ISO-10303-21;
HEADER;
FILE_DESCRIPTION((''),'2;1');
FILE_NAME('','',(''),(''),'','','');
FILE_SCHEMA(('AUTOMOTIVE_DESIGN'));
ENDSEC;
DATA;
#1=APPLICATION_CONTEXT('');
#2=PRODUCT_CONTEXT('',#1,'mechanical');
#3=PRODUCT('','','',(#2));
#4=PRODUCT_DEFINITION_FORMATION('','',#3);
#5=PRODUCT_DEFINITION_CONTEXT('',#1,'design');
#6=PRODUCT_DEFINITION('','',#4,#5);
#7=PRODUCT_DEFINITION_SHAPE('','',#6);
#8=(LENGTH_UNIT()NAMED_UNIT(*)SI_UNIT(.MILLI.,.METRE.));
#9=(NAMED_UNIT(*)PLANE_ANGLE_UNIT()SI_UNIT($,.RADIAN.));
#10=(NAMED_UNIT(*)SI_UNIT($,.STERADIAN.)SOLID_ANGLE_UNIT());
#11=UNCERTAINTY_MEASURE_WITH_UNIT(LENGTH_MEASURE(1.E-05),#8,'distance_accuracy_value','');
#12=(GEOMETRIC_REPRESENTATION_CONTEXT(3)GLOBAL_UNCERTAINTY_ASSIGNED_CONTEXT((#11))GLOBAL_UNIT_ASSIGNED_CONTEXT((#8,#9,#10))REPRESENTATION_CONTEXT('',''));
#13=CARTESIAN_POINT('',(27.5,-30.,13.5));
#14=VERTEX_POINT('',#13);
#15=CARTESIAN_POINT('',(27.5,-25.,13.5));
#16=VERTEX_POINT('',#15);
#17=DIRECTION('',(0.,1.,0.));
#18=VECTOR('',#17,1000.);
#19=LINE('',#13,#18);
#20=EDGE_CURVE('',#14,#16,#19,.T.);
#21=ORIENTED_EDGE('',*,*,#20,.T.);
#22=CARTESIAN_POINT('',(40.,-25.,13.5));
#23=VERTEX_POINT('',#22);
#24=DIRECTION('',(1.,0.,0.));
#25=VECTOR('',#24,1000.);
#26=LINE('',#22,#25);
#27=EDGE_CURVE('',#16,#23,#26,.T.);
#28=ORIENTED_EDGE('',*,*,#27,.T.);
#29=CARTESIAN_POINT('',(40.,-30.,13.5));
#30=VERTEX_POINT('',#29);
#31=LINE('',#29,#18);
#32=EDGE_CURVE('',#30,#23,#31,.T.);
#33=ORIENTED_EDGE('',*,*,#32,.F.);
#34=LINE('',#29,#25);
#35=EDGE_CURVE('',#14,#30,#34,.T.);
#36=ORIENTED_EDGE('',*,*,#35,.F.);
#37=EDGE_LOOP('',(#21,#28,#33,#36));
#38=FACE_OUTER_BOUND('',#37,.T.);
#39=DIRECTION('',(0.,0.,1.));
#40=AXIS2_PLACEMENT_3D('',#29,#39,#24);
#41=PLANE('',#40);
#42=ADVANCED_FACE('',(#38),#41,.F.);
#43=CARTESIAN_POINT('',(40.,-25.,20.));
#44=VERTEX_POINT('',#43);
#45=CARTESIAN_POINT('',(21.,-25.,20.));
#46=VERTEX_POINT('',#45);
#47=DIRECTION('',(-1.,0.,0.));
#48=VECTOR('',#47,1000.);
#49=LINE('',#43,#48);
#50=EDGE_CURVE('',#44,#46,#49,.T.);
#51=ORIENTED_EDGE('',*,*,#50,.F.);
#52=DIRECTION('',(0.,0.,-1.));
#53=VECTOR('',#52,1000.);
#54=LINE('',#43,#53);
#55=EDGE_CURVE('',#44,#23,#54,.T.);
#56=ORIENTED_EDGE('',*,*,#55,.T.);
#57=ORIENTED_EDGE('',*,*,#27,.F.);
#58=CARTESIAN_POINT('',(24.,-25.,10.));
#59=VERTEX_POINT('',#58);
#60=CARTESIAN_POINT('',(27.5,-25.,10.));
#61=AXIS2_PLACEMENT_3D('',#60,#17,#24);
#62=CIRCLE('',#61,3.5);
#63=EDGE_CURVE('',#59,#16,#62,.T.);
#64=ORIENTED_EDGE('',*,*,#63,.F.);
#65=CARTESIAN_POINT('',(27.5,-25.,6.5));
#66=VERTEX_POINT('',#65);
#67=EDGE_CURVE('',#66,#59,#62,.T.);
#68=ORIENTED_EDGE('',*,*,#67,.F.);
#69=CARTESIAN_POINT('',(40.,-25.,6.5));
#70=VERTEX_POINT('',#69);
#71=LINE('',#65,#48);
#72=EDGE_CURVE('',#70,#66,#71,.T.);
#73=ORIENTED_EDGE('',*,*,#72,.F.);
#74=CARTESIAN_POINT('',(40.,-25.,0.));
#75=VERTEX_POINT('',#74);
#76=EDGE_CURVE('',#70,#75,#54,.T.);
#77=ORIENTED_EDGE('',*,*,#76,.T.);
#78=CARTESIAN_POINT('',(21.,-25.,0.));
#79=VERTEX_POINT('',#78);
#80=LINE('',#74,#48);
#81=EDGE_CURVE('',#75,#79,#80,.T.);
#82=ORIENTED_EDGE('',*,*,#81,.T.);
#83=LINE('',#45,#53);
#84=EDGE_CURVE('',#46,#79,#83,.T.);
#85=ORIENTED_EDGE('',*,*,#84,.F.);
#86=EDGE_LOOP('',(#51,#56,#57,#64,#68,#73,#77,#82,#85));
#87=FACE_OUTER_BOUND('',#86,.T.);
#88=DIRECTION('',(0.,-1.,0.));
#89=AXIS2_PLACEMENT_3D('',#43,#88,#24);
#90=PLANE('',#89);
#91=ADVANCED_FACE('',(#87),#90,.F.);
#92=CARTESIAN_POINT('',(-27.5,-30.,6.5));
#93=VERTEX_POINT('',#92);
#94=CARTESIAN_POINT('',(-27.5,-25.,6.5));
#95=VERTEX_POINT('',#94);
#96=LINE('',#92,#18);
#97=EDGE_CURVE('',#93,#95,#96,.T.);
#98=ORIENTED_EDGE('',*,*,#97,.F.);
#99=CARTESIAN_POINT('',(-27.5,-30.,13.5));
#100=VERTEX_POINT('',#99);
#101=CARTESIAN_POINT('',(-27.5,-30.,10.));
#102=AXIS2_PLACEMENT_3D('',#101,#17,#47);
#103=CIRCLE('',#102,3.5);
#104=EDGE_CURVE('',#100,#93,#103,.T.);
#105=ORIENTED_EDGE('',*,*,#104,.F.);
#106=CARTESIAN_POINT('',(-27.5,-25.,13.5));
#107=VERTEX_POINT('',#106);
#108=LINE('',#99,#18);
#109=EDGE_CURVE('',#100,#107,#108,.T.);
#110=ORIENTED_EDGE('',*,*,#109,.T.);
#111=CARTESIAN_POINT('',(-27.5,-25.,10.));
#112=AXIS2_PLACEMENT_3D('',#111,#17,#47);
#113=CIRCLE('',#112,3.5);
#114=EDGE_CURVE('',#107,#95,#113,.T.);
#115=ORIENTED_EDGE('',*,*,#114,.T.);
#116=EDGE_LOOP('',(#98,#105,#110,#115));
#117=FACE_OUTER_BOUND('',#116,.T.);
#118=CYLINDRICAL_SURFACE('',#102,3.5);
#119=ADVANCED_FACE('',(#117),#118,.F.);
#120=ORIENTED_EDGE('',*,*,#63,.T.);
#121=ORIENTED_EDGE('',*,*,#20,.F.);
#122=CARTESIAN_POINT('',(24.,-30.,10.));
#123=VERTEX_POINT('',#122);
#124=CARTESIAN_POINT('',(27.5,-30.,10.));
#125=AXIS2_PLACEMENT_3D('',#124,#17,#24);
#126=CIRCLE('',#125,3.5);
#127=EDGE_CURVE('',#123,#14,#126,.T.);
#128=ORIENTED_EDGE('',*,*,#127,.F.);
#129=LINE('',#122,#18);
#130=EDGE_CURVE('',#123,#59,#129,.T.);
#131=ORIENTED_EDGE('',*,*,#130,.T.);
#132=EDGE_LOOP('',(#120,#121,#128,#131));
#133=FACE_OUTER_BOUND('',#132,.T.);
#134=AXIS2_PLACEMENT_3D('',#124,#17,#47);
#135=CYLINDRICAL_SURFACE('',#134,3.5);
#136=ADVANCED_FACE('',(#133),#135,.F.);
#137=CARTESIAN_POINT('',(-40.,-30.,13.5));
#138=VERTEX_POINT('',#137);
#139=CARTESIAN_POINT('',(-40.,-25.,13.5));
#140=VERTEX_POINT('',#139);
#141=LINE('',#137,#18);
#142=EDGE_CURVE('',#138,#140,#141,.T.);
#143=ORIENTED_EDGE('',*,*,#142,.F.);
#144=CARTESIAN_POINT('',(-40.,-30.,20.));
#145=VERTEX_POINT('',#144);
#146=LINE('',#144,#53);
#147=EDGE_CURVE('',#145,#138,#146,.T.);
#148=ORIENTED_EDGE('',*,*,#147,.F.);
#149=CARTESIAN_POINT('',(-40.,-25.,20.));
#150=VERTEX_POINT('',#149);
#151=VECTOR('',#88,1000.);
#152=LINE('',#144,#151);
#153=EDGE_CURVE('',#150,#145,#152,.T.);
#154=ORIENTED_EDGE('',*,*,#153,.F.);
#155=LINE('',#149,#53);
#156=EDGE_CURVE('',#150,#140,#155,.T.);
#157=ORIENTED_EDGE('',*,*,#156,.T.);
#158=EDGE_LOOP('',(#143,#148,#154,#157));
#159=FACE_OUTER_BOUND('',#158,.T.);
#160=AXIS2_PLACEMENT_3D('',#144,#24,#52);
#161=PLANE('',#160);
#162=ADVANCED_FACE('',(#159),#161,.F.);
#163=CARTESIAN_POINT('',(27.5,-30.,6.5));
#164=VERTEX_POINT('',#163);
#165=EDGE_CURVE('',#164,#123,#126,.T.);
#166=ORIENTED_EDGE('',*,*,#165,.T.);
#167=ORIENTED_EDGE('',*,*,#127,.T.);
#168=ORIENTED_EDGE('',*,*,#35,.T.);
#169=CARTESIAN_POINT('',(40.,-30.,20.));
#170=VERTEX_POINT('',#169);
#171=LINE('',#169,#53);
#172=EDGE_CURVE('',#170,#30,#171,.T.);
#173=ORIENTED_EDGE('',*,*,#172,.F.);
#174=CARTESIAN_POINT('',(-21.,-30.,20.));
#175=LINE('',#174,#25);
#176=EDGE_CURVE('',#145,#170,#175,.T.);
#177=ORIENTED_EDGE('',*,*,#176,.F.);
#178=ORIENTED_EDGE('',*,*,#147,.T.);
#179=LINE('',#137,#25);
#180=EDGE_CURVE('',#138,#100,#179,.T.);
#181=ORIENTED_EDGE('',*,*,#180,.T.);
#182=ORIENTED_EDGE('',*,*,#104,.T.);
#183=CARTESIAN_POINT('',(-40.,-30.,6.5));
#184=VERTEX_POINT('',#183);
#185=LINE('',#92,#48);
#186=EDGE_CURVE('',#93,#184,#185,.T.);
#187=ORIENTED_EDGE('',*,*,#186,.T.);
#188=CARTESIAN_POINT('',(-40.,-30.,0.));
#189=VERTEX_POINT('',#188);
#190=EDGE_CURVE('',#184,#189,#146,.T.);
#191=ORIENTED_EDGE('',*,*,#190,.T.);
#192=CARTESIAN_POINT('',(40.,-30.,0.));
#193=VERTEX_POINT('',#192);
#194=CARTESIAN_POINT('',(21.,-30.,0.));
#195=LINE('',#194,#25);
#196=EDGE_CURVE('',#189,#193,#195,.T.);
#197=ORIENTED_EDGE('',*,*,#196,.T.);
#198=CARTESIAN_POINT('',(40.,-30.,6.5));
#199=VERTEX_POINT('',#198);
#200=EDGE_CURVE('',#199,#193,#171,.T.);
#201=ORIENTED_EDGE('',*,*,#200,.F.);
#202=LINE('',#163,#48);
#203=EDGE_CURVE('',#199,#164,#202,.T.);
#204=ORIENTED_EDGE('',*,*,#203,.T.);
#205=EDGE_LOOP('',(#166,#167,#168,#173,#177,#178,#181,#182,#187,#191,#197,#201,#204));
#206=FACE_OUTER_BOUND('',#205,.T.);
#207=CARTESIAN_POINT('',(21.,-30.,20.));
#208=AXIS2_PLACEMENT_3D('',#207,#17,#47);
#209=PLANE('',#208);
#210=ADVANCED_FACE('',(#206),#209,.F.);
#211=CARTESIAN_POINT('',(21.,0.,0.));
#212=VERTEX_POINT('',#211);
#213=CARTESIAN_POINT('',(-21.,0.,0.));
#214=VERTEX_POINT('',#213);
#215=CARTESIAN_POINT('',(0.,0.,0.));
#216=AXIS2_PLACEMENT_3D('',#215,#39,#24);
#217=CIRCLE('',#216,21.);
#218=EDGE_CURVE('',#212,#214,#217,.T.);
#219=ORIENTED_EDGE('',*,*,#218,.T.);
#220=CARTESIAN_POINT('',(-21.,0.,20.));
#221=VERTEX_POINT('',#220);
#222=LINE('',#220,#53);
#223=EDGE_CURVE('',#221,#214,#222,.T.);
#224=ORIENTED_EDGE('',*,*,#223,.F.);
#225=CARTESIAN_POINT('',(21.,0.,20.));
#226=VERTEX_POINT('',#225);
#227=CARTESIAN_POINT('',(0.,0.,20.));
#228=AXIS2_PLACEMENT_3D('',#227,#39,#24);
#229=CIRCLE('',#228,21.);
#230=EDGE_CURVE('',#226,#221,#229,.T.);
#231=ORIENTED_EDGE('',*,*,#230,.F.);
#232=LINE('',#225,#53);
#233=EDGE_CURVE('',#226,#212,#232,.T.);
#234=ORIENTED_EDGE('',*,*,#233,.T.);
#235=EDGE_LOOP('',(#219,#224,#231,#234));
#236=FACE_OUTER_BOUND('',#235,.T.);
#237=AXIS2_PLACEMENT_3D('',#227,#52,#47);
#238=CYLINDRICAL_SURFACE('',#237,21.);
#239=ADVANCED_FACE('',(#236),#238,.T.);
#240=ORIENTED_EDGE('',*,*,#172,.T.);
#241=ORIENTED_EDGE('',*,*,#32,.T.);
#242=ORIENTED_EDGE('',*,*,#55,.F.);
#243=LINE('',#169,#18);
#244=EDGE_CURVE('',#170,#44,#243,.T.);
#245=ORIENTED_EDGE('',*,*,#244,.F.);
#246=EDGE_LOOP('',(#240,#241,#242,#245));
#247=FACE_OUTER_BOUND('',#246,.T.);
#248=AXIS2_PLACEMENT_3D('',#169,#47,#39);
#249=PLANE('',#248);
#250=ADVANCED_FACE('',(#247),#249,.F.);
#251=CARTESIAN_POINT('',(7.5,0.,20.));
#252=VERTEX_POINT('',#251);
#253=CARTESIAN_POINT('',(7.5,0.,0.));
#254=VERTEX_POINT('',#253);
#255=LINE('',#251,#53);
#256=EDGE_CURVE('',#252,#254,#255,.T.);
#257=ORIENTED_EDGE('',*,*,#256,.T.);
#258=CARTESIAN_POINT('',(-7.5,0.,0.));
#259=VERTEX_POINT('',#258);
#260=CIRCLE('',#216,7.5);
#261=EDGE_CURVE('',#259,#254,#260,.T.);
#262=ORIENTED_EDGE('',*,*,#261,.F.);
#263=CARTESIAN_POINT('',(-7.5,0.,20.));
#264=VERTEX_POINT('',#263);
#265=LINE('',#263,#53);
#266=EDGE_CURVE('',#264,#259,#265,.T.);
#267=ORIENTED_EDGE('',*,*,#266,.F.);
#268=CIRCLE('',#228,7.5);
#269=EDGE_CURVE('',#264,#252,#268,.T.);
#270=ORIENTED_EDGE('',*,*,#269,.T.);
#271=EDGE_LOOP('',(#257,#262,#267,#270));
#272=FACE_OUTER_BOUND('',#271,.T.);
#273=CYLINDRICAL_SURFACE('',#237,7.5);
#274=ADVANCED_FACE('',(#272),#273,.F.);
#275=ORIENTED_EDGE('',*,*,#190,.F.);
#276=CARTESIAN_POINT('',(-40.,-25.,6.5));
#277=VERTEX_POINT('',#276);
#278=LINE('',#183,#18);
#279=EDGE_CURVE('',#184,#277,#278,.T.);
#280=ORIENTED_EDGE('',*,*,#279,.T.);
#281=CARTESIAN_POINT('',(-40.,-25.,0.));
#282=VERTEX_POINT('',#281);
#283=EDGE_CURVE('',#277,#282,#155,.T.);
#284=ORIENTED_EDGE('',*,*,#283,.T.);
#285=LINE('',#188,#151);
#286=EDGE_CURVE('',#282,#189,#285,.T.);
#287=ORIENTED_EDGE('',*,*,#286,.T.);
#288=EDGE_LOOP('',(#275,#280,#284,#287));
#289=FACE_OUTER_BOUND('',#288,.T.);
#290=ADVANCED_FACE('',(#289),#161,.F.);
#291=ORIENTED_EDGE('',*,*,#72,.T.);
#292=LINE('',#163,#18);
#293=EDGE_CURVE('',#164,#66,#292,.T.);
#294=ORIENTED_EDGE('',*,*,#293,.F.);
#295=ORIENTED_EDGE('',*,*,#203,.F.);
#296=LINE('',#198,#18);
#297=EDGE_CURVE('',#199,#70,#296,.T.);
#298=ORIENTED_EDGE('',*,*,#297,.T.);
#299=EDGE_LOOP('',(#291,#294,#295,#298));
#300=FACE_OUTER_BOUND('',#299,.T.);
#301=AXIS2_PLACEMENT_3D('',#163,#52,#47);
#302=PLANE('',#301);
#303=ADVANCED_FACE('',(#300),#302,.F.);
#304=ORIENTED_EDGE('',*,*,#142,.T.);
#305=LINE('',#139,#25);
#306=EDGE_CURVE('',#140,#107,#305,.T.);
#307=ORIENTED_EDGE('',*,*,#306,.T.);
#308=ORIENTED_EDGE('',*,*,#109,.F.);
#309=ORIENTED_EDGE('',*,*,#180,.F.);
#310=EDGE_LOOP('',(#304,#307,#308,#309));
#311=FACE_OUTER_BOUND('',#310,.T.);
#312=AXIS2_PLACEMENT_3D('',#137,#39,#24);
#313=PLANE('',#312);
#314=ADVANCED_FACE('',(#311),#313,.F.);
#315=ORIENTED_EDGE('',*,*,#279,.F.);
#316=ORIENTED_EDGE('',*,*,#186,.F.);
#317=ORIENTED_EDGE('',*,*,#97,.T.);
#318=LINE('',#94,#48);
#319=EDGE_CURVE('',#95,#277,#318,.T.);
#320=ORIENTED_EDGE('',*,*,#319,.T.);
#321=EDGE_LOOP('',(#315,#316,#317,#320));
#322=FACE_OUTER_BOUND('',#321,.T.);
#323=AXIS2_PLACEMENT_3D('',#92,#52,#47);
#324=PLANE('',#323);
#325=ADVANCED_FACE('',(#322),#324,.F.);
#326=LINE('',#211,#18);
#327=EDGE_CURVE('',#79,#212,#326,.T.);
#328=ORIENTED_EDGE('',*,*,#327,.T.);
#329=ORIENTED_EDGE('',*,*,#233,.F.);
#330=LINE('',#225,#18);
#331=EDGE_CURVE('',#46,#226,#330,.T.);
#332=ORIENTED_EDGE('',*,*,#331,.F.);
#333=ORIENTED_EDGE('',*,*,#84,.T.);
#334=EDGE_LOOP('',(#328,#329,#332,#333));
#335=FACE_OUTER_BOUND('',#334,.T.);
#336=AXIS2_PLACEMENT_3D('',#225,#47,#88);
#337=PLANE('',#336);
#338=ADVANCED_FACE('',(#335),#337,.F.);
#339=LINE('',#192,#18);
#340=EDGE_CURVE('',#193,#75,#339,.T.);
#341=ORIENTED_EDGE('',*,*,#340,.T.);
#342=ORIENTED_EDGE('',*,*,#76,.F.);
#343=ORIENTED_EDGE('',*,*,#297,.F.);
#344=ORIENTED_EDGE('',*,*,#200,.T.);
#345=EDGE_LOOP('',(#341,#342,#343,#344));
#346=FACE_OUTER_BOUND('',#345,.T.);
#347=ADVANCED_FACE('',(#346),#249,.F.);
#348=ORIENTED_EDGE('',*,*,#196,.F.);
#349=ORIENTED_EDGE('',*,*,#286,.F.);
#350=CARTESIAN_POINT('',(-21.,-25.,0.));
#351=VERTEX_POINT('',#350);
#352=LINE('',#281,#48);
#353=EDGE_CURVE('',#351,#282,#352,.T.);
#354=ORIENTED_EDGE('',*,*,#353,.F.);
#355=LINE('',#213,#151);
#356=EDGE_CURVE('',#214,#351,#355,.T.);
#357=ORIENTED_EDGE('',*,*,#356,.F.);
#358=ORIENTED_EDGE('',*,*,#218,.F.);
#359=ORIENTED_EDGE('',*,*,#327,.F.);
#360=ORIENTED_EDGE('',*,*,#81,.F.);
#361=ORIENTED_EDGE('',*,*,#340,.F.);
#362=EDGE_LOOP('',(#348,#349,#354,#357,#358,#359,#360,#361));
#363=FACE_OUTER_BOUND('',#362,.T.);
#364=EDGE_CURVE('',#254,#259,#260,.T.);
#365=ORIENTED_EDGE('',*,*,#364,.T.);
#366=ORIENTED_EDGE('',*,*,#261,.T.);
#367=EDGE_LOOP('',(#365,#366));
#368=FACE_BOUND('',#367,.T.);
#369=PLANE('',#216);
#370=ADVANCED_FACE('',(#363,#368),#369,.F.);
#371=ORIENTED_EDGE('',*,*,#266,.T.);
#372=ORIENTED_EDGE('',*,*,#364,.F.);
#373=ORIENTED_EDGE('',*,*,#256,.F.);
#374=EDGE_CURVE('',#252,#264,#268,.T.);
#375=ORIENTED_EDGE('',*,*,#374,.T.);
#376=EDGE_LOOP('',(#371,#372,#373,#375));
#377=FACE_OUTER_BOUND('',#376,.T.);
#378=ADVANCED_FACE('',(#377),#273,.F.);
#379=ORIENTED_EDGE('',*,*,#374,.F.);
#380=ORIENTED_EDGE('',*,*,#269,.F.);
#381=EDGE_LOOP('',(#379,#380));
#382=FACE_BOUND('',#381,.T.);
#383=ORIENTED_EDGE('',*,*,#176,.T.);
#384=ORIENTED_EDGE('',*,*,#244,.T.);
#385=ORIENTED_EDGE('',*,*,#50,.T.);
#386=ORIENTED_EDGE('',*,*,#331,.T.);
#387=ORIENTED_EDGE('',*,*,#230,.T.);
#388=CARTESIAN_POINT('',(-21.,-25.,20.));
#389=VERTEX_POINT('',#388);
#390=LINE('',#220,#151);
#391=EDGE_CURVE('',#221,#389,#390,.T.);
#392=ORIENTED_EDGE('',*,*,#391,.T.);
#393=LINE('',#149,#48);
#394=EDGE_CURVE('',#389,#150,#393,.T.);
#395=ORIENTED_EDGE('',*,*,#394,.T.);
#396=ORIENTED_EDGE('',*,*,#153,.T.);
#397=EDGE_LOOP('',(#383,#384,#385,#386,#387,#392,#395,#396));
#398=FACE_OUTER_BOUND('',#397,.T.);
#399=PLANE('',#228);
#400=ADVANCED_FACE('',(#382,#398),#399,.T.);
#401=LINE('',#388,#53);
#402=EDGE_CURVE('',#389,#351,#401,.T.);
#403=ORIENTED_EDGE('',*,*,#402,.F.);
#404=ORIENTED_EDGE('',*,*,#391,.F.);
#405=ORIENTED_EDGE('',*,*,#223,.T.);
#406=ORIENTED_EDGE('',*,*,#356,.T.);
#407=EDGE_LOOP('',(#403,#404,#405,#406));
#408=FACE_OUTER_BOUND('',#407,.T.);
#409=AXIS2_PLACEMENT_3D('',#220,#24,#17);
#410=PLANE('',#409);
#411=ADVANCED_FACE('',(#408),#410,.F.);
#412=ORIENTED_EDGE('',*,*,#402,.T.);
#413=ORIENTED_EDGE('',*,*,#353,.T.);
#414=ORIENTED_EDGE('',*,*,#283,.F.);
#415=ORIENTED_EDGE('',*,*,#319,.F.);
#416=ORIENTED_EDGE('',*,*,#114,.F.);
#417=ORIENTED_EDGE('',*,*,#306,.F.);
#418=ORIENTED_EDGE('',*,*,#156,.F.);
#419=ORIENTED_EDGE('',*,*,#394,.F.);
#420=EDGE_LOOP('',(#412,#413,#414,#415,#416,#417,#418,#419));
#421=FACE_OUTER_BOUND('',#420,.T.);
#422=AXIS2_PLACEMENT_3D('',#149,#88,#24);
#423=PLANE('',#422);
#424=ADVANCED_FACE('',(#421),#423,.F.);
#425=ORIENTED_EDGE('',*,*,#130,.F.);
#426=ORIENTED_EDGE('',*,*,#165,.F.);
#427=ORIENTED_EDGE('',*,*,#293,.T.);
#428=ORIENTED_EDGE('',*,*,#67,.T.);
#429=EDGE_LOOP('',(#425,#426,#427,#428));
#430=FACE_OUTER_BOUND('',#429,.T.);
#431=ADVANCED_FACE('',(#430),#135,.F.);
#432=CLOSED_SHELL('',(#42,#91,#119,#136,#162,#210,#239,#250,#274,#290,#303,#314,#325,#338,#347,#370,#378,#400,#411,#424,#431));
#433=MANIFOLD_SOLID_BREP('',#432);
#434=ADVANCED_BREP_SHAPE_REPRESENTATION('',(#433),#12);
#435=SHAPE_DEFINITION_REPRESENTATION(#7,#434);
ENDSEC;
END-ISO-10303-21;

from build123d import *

# Parameters (mm, degrees)
SKETCH_1_R          = 7.5
EXTRUDE_1_DEPTH     = 20
CUT_EXTRUDE_1_DEPTH = 65.156059729


with BuildPart() as part:
    # 草图1 → 凸台-拉伸1 (new body)
    with BuildSketch(Plane.XY):
        with BuildLine():
            Line((21, 0), (21, -25))
            Line((21, -25), (40, -25))
            Line((40, -25), (40, -30))
            Line((40, -30), (21, -30))
            Line((21, -30), (-21, -30))
            Line((-21, -30), (-40, -30))
            Line((-40, -30), (-40, -25))
            Line((-40, -25), (-21, -25))
            Line((-21, -25), (-21, 0))
            ThreePointArc((-21, 0), (0, 21), (21, 0))
        make_face()
        Circle(SKETCH_1_R, mode=Mode.SUBTRACT)
    extrude(amount=EXTRUDE_1_DEPTH)

    # 草图2 → 切除-拉伸1 (cut, through all)
    with BuildSketch(Plane(origin=(0, -25, 0), x_dir=(1, 0, 0), z_dir=(0, 1, 0))):
        with BuildLine():
            Line((-27.5, -6.5), (-40, -6.5))
            Line((-40, -6.5), (-40, -13.5))
            Line((-40, -13.5), (-27.5, -13.5))
            ThreePointArc((-27.5, -13.5), (-24, -10), (-27.5, -6.5))
        make_face()
        with BuildLine():
            Line((40, -13.5), (27.5, -13.5))
            ThreePointArc((27.5, -13.5), (24, -10), (27.5, -6.5))
            Line((27.5, -6.5), (40, -6.5))
            Line((40, -6.5), (40, -13.5))
        make_face()
    extrude(amount=-CUT_EXTRUDE_1_DEPTH, mode=Mode.SUBTRACT)


solid = part.part
